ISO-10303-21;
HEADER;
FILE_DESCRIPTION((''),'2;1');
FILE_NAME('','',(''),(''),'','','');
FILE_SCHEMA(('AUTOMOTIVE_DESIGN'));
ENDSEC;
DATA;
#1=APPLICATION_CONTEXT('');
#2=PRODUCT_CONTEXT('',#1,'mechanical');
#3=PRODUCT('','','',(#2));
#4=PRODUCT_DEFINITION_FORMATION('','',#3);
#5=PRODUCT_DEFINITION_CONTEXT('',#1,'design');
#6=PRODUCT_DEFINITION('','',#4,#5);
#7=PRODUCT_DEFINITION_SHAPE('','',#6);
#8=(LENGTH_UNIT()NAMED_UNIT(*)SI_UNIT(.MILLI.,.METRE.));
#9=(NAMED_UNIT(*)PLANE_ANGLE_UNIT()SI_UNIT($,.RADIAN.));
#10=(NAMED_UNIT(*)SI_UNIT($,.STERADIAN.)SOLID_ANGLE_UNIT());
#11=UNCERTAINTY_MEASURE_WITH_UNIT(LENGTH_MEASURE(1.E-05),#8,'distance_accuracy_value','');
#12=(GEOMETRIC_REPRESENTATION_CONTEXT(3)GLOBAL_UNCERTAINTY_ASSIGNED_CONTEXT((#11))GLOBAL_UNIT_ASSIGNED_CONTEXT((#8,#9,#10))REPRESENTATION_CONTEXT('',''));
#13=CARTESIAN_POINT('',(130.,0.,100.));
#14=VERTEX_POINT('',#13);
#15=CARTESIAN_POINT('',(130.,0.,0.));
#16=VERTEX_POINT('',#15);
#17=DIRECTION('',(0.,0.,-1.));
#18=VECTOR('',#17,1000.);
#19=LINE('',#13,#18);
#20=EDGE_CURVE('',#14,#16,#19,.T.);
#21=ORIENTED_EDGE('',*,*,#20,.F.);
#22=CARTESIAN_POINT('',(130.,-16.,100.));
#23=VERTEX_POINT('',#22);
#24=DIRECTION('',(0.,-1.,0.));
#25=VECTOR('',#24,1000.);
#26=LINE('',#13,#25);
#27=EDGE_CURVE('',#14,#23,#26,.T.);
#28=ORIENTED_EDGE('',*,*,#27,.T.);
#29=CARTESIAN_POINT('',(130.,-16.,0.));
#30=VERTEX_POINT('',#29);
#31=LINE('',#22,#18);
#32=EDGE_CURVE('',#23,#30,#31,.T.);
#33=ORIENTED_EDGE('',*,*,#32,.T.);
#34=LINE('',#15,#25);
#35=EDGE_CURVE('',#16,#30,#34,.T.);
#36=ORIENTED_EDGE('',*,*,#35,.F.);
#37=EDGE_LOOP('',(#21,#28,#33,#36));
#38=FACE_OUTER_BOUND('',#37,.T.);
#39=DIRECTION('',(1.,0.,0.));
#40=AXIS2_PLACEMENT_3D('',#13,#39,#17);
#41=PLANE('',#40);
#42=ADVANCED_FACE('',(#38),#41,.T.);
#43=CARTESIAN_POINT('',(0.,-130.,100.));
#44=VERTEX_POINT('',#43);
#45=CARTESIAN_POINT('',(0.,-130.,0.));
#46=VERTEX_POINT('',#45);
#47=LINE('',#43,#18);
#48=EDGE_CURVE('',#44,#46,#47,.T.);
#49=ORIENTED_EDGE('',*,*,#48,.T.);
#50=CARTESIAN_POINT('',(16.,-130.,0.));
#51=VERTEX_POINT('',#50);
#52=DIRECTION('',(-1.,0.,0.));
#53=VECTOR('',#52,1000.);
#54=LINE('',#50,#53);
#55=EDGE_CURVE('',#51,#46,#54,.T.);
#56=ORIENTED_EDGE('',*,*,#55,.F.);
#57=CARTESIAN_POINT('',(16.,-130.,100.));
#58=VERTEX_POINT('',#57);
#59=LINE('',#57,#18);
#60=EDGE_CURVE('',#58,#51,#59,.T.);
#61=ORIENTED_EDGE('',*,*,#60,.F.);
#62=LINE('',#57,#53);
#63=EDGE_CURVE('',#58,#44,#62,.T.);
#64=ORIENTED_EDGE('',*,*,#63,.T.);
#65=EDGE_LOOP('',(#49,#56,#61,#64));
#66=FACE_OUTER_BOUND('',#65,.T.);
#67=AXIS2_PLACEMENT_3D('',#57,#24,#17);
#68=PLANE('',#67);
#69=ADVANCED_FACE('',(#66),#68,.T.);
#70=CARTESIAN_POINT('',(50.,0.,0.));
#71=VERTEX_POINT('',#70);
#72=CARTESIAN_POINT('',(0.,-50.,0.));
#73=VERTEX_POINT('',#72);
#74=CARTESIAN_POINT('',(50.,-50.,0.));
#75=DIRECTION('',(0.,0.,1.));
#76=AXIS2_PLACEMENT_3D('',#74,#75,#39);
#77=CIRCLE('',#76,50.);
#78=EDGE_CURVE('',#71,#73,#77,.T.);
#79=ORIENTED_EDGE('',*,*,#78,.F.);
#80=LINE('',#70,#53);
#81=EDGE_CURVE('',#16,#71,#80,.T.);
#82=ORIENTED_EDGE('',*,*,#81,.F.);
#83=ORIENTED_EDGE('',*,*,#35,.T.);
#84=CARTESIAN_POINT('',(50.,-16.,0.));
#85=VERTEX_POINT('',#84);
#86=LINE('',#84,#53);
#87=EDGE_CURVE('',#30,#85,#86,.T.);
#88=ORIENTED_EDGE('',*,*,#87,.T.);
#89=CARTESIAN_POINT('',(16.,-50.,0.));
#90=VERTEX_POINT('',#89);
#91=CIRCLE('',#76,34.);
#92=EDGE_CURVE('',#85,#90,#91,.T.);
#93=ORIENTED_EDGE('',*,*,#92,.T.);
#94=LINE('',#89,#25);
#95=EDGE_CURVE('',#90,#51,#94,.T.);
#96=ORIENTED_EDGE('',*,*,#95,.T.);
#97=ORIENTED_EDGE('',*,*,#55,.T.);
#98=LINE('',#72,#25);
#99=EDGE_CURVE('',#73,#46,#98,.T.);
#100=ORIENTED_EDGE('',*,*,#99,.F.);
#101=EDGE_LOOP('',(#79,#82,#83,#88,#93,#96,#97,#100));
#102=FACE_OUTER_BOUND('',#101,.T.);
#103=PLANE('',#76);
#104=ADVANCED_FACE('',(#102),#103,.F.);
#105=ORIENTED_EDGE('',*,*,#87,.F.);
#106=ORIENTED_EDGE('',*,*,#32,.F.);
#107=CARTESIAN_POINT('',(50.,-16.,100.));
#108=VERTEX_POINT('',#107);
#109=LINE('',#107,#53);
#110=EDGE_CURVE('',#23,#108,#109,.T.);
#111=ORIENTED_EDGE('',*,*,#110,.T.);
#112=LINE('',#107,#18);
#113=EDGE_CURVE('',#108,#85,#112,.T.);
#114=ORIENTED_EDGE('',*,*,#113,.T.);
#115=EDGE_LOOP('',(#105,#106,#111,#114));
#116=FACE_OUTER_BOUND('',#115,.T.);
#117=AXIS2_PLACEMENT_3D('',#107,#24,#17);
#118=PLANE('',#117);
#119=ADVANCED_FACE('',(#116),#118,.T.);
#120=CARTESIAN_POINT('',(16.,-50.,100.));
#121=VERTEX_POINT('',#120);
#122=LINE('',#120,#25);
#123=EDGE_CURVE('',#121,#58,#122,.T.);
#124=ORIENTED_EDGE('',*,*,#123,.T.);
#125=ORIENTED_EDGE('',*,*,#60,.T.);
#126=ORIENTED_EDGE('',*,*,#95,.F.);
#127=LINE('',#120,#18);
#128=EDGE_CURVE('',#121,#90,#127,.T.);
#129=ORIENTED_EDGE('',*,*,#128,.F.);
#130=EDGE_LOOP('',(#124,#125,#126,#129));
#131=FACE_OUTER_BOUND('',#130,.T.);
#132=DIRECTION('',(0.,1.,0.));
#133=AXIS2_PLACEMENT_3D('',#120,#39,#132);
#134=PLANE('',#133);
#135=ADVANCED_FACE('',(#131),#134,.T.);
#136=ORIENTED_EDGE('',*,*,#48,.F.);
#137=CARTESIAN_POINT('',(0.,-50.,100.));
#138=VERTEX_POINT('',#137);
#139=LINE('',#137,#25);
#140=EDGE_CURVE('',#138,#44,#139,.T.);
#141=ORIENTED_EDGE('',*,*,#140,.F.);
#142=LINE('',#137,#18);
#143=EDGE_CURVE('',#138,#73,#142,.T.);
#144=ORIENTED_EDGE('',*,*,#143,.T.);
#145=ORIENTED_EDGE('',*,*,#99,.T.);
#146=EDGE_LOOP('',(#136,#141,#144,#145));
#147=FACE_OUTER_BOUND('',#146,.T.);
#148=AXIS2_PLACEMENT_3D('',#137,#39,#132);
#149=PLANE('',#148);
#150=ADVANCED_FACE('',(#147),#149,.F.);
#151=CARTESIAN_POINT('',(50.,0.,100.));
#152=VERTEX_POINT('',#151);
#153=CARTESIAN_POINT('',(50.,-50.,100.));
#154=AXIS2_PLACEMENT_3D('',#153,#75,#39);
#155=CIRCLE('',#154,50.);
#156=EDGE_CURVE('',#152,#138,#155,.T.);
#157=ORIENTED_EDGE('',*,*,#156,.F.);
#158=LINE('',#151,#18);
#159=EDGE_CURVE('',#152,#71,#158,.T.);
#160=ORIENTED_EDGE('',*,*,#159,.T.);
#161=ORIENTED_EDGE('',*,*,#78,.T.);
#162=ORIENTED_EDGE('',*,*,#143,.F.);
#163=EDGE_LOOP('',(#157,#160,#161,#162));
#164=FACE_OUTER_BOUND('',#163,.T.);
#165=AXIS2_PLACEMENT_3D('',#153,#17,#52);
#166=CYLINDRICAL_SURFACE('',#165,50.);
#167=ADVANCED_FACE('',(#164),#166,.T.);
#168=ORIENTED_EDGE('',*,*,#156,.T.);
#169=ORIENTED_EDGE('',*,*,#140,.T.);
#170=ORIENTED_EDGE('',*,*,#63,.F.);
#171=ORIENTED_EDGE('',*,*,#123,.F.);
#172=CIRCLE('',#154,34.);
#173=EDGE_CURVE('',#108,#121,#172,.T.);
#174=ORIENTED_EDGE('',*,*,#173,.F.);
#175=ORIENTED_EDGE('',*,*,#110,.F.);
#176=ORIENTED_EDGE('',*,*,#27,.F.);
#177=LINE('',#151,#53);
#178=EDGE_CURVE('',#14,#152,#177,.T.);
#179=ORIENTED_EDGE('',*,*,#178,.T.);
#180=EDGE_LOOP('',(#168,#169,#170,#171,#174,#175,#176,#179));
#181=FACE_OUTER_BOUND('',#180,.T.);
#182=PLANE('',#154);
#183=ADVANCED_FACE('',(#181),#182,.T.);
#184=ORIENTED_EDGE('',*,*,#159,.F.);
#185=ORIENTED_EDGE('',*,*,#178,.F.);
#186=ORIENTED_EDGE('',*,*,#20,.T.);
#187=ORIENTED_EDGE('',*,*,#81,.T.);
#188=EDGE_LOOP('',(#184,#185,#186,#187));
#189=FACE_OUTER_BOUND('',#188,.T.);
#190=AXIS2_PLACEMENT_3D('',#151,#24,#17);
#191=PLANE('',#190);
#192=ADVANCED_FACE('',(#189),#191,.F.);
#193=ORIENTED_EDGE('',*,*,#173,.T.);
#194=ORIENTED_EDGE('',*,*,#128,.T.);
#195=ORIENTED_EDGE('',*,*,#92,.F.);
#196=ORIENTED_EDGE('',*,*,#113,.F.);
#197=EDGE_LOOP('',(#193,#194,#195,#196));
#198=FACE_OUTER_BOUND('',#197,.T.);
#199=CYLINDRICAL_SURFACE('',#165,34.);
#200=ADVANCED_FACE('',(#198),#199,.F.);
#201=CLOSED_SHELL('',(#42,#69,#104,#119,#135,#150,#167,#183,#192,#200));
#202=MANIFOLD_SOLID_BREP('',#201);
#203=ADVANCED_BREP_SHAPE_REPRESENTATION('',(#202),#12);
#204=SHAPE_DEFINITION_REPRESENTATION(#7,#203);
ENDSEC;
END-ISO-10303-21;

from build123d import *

# Parameters (mm, degrees)
EXTRUDE_THIN1_DEPTH = 100


with BuildPart() as part:
    # Sketch1 → Extrude-Thin1 (new body)
    with BuildSketch(Plane.XY):
        with BuildLine():
            Line((0, -130), (0, -50))
            ThreePointArc((0, -50), (14.644660941, -14.644660941), (50, 0))
            Line((50, 0), (130, 0))
            Line((130, 0), (130, -16))
            Line((130, -16), (50, -16))
            ThreePointArc((50, -16), (25.95836944, -25.95836944), (16, -50))
            Line((16, -50), (16, -130))
            Line((16, -130), (0, -130))
        make_face()
    extrude(amount=EXTRUDE_THIN1_DEPTH)


solid = part.part
